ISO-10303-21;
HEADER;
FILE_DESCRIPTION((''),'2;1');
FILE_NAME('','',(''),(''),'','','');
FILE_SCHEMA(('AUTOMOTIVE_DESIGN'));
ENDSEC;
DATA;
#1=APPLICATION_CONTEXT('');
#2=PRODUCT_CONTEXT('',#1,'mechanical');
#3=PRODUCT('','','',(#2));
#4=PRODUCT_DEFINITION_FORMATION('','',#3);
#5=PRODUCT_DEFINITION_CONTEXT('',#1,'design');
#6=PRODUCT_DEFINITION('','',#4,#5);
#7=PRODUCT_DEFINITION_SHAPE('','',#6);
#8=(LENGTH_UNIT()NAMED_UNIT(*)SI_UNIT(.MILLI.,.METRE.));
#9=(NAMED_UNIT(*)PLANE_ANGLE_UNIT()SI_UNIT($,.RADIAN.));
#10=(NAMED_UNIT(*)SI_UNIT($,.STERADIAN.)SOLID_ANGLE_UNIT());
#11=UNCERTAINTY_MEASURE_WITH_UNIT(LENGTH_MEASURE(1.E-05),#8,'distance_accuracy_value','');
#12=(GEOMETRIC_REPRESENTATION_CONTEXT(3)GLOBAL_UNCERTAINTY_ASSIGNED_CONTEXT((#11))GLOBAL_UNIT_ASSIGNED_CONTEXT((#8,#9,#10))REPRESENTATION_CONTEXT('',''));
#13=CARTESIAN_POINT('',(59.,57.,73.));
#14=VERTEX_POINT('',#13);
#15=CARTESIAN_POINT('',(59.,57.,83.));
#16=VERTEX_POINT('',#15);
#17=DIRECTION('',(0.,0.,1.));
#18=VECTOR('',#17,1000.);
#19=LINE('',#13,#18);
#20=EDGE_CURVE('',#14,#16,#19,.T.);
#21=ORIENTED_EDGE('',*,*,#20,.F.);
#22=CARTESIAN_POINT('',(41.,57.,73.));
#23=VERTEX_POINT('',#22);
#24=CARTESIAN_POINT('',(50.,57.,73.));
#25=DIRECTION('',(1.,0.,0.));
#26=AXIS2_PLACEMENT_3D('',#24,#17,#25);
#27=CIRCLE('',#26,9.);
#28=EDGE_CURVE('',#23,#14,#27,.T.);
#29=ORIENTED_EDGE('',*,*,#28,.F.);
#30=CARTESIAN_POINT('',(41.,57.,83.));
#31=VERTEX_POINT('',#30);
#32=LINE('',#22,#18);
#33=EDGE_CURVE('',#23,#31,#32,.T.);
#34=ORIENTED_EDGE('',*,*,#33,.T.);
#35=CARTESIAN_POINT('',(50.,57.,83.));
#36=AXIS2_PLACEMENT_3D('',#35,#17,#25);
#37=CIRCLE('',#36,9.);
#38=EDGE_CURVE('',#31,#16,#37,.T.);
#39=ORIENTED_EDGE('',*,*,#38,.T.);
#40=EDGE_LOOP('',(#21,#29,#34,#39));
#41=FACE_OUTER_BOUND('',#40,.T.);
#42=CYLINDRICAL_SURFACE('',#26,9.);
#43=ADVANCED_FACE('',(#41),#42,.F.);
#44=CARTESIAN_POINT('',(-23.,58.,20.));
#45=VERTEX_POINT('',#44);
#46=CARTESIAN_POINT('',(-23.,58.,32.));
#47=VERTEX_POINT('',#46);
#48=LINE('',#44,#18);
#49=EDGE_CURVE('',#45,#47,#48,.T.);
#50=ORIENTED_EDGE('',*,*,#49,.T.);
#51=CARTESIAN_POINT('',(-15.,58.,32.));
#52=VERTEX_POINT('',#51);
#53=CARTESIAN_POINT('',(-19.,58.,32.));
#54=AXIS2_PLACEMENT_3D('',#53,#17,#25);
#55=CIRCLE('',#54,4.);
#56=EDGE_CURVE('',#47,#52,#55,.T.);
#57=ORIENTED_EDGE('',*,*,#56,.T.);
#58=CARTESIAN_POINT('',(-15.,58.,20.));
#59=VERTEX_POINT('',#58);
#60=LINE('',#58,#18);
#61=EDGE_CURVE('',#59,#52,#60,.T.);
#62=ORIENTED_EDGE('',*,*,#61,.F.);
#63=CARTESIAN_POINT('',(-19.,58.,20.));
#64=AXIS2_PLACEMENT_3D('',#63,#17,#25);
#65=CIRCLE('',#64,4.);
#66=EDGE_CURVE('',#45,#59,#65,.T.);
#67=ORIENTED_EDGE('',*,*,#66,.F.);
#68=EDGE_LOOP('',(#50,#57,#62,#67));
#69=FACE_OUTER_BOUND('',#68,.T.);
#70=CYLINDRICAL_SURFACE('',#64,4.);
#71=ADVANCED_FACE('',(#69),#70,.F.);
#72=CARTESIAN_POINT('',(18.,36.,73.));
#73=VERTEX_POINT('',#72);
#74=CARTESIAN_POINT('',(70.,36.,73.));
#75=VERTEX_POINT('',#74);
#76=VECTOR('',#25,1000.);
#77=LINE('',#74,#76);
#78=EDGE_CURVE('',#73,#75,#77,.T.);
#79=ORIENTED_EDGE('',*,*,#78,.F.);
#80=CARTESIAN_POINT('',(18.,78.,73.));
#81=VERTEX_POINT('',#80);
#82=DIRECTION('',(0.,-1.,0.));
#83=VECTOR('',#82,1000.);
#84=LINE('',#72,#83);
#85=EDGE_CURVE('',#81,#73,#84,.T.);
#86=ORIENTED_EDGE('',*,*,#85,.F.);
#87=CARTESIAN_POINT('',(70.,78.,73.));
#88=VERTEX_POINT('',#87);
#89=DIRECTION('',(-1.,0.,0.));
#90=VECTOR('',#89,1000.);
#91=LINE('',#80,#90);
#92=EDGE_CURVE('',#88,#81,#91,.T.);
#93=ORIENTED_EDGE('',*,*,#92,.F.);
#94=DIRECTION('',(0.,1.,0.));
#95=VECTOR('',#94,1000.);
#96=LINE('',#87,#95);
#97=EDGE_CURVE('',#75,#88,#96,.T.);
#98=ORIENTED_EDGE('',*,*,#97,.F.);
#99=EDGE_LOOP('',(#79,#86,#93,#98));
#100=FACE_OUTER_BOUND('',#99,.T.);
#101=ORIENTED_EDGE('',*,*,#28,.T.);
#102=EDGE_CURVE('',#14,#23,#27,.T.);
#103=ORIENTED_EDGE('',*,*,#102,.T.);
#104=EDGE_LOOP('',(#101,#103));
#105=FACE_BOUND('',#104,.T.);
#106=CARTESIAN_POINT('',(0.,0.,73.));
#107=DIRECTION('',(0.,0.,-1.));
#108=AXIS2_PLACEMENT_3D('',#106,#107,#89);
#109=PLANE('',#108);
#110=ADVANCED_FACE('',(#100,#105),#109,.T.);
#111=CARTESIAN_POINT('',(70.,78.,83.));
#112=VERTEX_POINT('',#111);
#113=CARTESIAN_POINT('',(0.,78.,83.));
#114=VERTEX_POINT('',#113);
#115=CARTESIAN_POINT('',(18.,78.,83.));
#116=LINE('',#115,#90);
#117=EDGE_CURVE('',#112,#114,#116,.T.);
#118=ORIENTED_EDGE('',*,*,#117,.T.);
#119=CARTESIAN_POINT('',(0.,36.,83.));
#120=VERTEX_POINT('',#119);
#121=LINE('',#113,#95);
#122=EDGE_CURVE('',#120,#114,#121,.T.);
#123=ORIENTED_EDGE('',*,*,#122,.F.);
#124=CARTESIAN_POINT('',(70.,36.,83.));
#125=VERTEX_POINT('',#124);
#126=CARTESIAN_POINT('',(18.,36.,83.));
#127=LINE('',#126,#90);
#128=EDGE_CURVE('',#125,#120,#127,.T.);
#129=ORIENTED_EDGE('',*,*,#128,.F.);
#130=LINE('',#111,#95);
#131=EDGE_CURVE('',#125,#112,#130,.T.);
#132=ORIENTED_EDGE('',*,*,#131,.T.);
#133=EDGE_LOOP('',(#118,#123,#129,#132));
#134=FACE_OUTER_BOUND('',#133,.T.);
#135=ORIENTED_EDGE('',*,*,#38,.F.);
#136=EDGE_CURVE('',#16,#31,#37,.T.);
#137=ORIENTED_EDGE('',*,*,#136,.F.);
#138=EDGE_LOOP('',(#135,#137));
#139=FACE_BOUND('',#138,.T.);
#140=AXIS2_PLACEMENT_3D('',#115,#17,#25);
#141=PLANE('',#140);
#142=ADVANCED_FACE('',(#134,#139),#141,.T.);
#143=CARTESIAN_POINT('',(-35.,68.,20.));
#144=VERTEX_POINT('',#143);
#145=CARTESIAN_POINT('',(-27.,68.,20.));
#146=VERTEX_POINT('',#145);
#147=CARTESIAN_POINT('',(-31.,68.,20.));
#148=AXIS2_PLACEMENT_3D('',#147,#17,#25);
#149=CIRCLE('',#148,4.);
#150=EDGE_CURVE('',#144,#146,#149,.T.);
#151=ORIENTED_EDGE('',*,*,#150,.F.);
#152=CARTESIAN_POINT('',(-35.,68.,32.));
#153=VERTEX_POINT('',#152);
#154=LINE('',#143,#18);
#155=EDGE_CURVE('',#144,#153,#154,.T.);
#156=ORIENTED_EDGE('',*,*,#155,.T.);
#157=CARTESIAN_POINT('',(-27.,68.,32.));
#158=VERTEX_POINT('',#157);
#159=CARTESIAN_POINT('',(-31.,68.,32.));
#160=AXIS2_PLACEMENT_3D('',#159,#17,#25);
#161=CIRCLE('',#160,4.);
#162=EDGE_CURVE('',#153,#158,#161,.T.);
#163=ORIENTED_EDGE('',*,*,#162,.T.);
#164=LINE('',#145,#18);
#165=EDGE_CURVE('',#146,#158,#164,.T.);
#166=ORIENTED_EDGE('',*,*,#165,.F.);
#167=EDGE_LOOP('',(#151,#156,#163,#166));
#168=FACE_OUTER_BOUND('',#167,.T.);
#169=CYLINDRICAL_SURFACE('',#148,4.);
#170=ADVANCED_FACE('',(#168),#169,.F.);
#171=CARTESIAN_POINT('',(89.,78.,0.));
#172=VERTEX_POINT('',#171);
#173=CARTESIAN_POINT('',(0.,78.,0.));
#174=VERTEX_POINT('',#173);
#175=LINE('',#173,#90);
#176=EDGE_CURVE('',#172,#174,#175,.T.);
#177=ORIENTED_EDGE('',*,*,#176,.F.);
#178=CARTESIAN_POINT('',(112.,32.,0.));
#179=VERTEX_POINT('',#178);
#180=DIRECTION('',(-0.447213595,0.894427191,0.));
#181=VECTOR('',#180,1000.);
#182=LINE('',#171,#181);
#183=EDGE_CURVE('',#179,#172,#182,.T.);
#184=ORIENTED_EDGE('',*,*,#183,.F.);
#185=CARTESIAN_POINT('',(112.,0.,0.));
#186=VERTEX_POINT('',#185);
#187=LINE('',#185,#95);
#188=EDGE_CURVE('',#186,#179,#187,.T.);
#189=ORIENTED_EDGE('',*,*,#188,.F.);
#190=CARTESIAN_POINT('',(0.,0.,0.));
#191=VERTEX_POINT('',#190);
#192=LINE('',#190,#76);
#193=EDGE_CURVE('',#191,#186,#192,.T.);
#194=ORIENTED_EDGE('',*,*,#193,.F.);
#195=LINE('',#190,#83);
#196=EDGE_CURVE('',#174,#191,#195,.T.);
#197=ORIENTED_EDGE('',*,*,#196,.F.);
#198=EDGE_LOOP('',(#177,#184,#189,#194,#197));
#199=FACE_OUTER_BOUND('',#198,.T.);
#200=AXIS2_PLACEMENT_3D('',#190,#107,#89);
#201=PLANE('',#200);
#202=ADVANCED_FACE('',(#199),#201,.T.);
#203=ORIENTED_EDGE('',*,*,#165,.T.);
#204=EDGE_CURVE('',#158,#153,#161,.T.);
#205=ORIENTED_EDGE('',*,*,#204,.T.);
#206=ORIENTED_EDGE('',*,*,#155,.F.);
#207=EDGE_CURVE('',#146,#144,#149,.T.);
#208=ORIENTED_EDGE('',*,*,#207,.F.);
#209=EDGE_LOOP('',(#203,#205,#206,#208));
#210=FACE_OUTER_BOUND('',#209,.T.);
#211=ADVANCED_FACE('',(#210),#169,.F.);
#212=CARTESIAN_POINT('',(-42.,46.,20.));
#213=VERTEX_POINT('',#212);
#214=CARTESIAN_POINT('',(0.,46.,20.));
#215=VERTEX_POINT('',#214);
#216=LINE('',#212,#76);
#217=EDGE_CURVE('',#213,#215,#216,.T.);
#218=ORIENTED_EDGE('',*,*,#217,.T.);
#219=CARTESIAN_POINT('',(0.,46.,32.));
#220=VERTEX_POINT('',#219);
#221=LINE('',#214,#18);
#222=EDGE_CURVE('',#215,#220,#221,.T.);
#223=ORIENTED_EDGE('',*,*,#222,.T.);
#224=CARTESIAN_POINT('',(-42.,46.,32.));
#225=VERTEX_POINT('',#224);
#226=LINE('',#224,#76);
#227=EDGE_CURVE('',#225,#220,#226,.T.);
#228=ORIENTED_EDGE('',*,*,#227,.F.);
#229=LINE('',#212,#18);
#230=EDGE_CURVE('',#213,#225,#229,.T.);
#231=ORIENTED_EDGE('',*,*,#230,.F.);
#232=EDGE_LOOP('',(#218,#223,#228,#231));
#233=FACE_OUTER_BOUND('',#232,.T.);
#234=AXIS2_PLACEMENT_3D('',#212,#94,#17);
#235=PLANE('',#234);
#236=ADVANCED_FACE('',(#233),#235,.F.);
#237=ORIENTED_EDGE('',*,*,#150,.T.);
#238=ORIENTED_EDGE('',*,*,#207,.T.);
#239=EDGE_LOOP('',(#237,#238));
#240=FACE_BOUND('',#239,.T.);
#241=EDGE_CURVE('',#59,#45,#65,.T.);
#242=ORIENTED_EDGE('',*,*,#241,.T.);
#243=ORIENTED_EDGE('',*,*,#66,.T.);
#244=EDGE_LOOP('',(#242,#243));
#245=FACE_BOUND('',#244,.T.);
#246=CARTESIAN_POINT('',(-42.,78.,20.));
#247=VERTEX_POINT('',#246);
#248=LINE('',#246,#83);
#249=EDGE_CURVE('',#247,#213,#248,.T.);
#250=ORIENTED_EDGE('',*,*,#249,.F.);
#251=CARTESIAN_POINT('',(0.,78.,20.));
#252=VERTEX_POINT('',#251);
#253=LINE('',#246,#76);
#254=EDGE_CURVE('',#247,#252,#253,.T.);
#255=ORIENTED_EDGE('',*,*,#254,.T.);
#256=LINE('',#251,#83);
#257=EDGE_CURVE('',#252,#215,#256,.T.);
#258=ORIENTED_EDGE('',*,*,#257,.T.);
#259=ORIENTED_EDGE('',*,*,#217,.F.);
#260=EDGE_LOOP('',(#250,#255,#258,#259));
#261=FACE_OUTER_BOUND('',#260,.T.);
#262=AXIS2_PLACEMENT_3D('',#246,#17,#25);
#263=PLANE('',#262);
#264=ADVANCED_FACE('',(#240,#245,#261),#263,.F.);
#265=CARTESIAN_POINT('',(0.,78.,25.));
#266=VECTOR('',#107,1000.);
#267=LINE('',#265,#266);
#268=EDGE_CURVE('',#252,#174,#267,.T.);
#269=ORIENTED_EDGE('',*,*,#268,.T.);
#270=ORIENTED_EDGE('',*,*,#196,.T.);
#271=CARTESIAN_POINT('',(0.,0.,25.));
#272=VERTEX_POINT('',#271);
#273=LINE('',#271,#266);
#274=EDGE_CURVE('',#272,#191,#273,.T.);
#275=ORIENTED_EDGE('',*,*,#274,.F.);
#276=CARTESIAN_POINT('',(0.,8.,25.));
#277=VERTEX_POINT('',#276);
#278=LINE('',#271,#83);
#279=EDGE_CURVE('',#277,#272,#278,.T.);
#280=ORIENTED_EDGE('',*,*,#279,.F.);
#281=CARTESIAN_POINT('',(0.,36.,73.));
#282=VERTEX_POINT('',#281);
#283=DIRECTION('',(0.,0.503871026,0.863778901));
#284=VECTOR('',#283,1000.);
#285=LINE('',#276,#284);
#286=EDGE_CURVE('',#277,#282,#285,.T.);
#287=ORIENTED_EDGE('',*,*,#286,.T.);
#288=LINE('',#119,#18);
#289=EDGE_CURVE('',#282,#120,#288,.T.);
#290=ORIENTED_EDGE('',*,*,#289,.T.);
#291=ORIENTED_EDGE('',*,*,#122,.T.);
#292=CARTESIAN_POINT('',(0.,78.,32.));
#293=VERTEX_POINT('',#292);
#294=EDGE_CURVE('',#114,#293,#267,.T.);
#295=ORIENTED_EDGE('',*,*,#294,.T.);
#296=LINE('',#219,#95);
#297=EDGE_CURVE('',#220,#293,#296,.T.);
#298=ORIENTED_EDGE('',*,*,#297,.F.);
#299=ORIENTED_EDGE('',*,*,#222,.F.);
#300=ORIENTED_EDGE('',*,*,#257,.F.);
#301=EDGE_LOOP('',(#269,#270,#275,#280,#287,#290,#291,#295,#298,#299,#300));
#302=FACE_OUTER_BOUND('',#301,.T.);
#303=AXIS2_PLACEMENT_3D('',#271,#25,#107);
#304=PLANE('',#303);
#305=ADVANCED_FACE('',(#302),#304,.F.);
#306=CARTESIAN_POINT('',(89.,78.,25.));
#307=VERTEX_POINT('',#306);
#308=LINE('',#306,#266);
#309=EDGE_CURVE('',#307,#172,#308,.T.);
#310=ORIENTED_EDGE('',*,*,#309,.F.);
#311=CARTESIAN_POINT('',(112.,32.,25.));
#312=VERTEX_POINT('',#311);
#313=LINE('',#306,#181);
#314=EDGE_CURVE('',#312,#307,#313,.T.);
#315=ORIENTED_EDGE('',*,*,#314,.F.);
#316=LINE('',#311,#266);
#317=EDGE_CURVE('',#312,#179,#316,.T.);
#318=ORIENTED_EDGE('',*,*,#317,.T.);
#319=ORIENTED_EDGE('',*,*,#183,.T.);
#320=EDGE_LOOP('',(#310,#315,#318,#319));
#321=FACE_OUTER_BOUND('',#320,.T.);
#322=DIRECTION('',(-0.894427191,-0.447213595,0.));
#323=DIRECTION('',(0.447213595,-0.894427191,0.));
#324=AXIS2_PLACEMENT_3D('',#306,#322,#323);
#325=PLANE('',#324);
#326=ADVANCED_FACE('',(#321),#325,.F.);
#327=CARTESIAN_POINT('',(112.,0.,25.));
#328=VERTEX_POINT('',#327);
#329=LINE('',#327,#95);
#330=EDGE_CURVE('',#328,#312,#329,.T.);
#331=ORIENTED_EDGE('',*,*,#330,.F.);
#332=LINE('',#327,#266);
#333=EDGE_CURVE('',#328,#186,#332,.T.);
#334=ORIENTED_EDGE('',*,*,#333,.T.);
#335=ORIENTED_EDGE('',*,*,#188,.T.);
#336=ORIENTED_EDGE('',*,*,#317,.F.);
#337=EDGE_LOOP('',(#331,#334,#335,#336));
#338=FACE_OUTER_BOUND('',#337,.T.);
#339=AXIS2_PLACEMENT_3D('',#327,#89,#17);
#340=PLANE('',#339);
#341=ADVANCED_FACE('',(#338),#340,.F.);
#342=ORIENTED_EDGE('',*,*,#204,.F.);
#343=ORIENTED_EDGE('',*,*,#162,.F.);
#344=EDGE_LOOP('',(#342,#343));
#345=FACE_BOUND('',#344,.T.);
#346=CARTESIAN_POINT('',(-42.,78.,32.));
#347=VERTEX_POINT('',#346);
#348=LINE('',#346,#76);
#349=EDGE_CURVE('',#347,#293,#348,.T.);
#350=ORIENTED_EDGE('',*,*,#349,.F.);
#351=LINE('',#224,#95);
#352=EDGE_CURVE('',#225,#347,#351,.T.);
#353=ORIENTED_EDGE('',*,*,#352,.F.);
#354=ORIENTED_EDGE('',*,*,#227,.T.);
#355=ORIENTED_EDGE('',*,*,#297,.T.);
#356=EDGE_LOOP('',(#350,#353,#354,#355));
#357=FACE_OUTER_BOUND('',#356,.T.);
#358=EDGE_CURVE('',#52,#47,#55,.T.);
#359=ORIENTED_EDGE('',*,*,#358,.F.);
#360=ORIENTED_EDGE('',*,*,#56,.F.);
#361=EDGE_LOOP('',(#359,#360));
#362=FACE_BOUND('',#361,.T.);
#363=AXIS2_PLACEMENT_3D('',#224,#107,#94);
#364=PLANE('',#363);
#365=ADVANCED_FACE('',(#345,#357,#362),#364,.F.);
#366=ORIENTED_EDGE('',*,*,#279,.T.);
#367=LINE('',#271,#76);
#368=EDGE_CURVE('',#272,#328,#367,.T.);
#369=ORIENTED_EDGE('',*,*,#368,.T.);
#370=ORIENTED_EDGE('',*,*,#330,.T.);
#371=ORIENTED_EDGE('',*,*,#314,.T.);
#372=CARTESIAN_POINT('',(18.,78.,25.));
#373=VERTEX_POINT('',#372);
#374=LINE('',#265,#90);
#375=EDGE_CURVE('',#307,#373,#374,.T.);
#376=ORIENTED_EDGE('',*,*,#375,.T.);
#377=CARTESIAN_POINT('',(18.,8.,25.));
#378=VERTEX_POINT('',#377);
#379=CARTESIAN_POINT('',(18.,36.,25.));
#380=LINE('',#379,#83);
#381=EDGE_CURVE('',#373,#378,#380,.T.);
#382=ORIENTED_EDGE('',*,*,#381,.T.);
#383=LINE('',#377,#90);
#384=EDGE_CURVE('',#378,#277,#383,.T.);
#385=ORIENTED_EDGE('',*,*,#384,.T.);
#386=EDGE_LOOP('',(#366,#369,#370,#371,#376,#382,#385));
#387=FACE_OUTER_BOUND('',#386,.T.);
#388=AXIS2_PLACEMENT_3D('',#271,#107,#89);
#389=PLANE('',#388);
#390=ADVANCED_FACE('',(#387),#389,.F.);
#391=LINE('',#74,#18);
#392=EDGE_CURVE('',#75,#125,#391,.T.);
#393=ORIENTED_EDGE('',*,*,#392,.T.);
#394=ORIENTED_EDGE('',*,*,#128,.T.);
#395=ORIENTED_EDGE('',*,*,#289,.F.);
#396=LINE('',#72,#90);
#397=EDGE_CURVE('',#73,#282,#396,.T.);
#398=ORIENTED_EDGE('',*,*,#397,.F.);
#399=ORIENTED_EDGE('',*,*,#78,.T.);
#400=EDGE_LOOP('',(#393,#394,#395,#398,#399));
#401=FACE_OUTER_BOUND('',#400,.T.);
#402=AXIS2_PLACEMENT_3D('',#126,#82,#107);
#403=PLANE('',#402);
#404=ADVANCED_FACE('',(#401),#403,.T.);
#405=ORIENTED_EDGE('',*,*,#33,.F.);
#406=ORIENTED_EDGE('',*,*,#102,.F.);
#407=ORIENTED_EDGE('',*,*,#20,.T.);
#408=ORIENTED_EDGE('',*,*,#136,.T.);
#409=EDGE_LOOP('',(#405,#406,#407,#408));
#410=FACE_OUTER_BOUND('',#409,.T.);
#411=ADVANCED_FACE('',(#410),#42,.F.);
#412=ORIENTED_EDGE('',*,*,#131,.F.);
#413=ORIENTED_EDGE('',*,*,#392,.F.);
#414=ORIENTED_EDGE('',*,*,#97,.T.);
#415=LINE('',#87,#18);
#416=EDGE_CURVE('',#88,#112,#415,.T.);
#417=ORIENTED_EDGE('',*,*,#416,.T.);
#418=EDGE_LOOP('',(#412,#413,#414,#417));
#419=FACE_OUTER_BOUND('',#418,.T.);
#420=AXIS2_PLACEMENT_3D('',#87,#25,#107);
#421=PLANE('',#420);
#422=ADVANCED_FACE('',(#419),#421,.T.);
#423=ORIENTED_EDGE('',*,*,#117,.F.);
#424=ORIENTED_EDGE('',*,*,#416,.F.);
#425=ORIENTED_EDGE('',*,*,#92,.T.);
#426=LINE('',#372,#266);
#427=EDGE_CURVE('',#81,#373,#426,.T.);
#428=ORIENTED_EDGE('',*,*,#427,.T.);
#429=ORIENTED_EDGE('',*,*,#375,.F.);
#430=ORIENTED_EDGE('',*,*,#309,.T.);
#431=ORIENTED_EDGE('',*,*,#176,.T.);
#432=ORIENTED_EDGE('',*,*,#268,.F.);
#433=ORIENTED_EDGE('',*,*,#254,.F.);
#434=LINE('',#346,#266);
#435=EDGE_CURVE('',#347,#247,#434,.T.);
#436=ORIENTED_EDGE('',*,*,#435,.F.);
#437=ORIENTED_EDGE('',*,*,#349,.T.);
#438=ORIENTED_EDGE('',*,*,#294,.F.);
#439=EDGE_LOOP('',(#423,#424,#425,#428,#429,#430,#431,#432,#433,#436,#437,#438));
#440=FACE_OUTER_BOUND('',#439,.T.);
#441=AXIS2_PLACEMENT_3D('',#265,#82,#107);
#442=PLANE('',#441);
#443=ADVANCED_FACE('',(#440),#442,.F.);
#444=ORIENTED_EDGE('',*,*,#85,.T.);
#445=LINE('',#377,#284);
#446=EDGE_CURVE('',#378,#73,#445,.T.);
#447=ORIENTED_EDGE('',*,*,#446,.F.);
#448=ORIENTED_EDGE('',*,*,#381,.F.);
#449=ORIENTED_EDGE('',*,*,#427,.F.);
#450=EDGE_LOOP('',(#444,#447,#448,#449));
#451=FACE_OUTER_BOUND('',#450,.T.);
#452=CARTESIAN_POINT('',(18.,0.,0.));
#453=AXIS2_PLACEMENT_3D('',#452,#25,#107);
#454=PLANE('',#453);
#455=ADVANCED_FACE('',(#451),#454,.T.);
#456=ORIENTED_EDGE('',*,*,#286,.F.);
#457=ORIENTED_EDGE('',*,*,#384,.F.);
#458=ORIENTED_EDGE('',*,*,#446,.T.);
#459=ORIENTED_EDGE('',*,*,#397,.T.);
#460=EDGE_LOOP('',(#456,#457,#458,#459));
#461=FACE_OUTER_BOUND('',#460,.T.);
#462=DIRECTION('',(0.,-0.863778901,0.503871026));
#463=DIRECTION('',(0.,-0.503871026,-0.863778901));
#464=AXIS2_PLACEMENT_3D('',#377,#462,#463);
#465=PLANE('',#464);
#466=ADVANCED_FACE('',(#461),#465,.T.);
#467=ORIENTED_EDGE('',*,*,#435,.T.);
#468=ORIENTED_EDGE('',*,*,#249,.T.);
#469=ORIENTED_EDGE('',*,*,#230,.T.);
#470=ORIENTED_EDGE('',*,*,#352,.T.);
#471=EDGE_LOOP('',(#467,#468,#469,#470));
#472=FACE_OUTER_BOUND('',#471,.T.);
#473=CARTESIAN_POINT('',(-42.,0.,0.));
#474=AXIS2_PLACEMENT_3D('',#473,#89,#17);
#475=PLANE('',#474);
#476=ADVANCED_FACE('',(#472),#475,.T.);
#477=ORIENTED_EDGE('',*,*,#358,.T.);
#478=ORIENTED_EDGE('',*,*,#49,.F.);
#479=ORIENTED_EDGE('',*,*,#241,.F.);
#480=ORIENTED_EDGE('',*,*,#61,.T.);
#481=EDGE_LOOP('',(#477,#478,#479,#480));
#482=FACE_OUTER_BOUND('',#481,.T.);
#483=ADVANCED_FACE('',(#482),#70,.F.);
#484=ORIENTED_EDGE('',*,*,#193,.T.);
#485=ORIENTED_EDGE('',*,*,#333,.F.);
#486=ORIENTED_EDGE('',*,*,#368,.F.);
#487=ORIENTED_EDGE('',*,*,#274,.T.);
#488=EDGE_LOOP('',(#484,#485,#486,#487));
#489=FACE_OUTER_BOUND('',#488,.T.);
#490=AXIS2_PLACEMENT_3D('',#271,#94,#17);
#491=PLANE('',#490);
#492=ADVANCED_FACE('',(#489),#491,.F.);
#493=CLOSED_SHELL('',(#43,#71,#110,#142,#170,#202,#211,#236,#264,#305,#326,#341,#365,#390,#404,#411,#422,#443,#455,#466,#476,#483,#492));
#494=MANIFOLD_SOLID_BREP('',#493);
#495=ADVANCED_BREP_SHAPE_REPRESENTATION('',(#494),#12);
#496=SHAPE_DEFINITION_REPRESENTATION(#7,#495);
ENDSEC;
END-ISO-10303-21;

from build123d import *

# Parameters (mm, degrees)
BASE_BLOCK_DEPTH          = 25
UPRIGHT_BLOCK_DEPTH       = 18
SIDE_TAB_SKETCH_W         = 12
SIDE_TAB_SKETCH_H         = 32
SIDE_TAB_DEPTH            = 42
FRONT_PLATE_SKETCH_W      = 52
FRONT_PLATE_SKETCH_H      = 42
FRONT_PLATE_DEPTH         = 10
FRONT_PLATE_HOLE_SKETCH_R = 9
FRONT_PLATE_HOLE_DEPTH    = 10
SIDE_TAB_HOLES_SKETCH_R   = 4
SIDE_TAB_HOLES_2X_DEPTH   = 12
TRIANGULAR_GUSSET_DEPTH   = 18


with BuildPart() as part:
    # Base Block Sketch → Base Block (new body)
    with BuildSketch(Plane.XY):
        Polygon((0, 0), (112, 0), (112, 32), (89, 78), (0, 78), align=None)
    extrude(amount=BASE_BLOCK_DEPTH)

    # Upright Block Sketch → Upright Block (add)
    with BuildSketch(Plane.ZY):
        Polygon((71, 36), (25, 36), (25, 78), (83, 78), (83, 36), align=None)
    extrude(amount=-UPRIGHT_BLOCK_DEPTH)

    # Side Tab Sketch → Side Tab (add)
    with BuildSketch(Plane.ZY):
        with Locations((26, 62)):
            Rectangle(SIDE_TAB_SKETCH_W, SIDE_TAB_SKETCH_H)
    extrude(amount=SIDE_TAB_DEPTH)

    # Front Plate Sketch → Front Plate (add)
    with BuildSketch(Plane.XY.offset(83)):
        with Locations((44, 57)):
            Rectangle(FRONT_PLATE_SKETCH_W, FRONT_PLATE_SKETCH_H)
    extrude(amount=-FRONT_PLATE_DEPTH)

    # Front Plate Hole Sketch → Front Plate Hole (cut)
    with BuildSketch(Plane.XY.offset(83)):
        with Locations((50, 57)):
            Circle(FRONT_PLATE_HOLE_SKETCH_R)
    extrude(amount=-FRONT_PLATE_HOLE_DEPTH, mode=Mode.SUBTRACT)

    # Side Tab Holes Sketch → Side Tab Holes 2x (cut)
    with BuildSketch(Plane.XY.offset(32)):
        with Locations((-31, 68)):
            Circle(SIDE_TAB_HOLES_SKETCH_R)
        with Locations((-19, 58)):
            Circle(SIDE_TAB_HOLES_SKETCH_R)
    extrude(amount=-SIDE_TAB_HOLES_2X_DEPTH, mode=Mode.SUBTRACT)

    # Gusset Sketch → Triangular Gusset (add)
    with BuildSketch(Plane.ZY):
        Polygon((25, 36), (73, 36), (25, 8), align=None)
    extrude(amount=-TRIANGULAR_GUSSET_DEPTH)


solid = part.part
